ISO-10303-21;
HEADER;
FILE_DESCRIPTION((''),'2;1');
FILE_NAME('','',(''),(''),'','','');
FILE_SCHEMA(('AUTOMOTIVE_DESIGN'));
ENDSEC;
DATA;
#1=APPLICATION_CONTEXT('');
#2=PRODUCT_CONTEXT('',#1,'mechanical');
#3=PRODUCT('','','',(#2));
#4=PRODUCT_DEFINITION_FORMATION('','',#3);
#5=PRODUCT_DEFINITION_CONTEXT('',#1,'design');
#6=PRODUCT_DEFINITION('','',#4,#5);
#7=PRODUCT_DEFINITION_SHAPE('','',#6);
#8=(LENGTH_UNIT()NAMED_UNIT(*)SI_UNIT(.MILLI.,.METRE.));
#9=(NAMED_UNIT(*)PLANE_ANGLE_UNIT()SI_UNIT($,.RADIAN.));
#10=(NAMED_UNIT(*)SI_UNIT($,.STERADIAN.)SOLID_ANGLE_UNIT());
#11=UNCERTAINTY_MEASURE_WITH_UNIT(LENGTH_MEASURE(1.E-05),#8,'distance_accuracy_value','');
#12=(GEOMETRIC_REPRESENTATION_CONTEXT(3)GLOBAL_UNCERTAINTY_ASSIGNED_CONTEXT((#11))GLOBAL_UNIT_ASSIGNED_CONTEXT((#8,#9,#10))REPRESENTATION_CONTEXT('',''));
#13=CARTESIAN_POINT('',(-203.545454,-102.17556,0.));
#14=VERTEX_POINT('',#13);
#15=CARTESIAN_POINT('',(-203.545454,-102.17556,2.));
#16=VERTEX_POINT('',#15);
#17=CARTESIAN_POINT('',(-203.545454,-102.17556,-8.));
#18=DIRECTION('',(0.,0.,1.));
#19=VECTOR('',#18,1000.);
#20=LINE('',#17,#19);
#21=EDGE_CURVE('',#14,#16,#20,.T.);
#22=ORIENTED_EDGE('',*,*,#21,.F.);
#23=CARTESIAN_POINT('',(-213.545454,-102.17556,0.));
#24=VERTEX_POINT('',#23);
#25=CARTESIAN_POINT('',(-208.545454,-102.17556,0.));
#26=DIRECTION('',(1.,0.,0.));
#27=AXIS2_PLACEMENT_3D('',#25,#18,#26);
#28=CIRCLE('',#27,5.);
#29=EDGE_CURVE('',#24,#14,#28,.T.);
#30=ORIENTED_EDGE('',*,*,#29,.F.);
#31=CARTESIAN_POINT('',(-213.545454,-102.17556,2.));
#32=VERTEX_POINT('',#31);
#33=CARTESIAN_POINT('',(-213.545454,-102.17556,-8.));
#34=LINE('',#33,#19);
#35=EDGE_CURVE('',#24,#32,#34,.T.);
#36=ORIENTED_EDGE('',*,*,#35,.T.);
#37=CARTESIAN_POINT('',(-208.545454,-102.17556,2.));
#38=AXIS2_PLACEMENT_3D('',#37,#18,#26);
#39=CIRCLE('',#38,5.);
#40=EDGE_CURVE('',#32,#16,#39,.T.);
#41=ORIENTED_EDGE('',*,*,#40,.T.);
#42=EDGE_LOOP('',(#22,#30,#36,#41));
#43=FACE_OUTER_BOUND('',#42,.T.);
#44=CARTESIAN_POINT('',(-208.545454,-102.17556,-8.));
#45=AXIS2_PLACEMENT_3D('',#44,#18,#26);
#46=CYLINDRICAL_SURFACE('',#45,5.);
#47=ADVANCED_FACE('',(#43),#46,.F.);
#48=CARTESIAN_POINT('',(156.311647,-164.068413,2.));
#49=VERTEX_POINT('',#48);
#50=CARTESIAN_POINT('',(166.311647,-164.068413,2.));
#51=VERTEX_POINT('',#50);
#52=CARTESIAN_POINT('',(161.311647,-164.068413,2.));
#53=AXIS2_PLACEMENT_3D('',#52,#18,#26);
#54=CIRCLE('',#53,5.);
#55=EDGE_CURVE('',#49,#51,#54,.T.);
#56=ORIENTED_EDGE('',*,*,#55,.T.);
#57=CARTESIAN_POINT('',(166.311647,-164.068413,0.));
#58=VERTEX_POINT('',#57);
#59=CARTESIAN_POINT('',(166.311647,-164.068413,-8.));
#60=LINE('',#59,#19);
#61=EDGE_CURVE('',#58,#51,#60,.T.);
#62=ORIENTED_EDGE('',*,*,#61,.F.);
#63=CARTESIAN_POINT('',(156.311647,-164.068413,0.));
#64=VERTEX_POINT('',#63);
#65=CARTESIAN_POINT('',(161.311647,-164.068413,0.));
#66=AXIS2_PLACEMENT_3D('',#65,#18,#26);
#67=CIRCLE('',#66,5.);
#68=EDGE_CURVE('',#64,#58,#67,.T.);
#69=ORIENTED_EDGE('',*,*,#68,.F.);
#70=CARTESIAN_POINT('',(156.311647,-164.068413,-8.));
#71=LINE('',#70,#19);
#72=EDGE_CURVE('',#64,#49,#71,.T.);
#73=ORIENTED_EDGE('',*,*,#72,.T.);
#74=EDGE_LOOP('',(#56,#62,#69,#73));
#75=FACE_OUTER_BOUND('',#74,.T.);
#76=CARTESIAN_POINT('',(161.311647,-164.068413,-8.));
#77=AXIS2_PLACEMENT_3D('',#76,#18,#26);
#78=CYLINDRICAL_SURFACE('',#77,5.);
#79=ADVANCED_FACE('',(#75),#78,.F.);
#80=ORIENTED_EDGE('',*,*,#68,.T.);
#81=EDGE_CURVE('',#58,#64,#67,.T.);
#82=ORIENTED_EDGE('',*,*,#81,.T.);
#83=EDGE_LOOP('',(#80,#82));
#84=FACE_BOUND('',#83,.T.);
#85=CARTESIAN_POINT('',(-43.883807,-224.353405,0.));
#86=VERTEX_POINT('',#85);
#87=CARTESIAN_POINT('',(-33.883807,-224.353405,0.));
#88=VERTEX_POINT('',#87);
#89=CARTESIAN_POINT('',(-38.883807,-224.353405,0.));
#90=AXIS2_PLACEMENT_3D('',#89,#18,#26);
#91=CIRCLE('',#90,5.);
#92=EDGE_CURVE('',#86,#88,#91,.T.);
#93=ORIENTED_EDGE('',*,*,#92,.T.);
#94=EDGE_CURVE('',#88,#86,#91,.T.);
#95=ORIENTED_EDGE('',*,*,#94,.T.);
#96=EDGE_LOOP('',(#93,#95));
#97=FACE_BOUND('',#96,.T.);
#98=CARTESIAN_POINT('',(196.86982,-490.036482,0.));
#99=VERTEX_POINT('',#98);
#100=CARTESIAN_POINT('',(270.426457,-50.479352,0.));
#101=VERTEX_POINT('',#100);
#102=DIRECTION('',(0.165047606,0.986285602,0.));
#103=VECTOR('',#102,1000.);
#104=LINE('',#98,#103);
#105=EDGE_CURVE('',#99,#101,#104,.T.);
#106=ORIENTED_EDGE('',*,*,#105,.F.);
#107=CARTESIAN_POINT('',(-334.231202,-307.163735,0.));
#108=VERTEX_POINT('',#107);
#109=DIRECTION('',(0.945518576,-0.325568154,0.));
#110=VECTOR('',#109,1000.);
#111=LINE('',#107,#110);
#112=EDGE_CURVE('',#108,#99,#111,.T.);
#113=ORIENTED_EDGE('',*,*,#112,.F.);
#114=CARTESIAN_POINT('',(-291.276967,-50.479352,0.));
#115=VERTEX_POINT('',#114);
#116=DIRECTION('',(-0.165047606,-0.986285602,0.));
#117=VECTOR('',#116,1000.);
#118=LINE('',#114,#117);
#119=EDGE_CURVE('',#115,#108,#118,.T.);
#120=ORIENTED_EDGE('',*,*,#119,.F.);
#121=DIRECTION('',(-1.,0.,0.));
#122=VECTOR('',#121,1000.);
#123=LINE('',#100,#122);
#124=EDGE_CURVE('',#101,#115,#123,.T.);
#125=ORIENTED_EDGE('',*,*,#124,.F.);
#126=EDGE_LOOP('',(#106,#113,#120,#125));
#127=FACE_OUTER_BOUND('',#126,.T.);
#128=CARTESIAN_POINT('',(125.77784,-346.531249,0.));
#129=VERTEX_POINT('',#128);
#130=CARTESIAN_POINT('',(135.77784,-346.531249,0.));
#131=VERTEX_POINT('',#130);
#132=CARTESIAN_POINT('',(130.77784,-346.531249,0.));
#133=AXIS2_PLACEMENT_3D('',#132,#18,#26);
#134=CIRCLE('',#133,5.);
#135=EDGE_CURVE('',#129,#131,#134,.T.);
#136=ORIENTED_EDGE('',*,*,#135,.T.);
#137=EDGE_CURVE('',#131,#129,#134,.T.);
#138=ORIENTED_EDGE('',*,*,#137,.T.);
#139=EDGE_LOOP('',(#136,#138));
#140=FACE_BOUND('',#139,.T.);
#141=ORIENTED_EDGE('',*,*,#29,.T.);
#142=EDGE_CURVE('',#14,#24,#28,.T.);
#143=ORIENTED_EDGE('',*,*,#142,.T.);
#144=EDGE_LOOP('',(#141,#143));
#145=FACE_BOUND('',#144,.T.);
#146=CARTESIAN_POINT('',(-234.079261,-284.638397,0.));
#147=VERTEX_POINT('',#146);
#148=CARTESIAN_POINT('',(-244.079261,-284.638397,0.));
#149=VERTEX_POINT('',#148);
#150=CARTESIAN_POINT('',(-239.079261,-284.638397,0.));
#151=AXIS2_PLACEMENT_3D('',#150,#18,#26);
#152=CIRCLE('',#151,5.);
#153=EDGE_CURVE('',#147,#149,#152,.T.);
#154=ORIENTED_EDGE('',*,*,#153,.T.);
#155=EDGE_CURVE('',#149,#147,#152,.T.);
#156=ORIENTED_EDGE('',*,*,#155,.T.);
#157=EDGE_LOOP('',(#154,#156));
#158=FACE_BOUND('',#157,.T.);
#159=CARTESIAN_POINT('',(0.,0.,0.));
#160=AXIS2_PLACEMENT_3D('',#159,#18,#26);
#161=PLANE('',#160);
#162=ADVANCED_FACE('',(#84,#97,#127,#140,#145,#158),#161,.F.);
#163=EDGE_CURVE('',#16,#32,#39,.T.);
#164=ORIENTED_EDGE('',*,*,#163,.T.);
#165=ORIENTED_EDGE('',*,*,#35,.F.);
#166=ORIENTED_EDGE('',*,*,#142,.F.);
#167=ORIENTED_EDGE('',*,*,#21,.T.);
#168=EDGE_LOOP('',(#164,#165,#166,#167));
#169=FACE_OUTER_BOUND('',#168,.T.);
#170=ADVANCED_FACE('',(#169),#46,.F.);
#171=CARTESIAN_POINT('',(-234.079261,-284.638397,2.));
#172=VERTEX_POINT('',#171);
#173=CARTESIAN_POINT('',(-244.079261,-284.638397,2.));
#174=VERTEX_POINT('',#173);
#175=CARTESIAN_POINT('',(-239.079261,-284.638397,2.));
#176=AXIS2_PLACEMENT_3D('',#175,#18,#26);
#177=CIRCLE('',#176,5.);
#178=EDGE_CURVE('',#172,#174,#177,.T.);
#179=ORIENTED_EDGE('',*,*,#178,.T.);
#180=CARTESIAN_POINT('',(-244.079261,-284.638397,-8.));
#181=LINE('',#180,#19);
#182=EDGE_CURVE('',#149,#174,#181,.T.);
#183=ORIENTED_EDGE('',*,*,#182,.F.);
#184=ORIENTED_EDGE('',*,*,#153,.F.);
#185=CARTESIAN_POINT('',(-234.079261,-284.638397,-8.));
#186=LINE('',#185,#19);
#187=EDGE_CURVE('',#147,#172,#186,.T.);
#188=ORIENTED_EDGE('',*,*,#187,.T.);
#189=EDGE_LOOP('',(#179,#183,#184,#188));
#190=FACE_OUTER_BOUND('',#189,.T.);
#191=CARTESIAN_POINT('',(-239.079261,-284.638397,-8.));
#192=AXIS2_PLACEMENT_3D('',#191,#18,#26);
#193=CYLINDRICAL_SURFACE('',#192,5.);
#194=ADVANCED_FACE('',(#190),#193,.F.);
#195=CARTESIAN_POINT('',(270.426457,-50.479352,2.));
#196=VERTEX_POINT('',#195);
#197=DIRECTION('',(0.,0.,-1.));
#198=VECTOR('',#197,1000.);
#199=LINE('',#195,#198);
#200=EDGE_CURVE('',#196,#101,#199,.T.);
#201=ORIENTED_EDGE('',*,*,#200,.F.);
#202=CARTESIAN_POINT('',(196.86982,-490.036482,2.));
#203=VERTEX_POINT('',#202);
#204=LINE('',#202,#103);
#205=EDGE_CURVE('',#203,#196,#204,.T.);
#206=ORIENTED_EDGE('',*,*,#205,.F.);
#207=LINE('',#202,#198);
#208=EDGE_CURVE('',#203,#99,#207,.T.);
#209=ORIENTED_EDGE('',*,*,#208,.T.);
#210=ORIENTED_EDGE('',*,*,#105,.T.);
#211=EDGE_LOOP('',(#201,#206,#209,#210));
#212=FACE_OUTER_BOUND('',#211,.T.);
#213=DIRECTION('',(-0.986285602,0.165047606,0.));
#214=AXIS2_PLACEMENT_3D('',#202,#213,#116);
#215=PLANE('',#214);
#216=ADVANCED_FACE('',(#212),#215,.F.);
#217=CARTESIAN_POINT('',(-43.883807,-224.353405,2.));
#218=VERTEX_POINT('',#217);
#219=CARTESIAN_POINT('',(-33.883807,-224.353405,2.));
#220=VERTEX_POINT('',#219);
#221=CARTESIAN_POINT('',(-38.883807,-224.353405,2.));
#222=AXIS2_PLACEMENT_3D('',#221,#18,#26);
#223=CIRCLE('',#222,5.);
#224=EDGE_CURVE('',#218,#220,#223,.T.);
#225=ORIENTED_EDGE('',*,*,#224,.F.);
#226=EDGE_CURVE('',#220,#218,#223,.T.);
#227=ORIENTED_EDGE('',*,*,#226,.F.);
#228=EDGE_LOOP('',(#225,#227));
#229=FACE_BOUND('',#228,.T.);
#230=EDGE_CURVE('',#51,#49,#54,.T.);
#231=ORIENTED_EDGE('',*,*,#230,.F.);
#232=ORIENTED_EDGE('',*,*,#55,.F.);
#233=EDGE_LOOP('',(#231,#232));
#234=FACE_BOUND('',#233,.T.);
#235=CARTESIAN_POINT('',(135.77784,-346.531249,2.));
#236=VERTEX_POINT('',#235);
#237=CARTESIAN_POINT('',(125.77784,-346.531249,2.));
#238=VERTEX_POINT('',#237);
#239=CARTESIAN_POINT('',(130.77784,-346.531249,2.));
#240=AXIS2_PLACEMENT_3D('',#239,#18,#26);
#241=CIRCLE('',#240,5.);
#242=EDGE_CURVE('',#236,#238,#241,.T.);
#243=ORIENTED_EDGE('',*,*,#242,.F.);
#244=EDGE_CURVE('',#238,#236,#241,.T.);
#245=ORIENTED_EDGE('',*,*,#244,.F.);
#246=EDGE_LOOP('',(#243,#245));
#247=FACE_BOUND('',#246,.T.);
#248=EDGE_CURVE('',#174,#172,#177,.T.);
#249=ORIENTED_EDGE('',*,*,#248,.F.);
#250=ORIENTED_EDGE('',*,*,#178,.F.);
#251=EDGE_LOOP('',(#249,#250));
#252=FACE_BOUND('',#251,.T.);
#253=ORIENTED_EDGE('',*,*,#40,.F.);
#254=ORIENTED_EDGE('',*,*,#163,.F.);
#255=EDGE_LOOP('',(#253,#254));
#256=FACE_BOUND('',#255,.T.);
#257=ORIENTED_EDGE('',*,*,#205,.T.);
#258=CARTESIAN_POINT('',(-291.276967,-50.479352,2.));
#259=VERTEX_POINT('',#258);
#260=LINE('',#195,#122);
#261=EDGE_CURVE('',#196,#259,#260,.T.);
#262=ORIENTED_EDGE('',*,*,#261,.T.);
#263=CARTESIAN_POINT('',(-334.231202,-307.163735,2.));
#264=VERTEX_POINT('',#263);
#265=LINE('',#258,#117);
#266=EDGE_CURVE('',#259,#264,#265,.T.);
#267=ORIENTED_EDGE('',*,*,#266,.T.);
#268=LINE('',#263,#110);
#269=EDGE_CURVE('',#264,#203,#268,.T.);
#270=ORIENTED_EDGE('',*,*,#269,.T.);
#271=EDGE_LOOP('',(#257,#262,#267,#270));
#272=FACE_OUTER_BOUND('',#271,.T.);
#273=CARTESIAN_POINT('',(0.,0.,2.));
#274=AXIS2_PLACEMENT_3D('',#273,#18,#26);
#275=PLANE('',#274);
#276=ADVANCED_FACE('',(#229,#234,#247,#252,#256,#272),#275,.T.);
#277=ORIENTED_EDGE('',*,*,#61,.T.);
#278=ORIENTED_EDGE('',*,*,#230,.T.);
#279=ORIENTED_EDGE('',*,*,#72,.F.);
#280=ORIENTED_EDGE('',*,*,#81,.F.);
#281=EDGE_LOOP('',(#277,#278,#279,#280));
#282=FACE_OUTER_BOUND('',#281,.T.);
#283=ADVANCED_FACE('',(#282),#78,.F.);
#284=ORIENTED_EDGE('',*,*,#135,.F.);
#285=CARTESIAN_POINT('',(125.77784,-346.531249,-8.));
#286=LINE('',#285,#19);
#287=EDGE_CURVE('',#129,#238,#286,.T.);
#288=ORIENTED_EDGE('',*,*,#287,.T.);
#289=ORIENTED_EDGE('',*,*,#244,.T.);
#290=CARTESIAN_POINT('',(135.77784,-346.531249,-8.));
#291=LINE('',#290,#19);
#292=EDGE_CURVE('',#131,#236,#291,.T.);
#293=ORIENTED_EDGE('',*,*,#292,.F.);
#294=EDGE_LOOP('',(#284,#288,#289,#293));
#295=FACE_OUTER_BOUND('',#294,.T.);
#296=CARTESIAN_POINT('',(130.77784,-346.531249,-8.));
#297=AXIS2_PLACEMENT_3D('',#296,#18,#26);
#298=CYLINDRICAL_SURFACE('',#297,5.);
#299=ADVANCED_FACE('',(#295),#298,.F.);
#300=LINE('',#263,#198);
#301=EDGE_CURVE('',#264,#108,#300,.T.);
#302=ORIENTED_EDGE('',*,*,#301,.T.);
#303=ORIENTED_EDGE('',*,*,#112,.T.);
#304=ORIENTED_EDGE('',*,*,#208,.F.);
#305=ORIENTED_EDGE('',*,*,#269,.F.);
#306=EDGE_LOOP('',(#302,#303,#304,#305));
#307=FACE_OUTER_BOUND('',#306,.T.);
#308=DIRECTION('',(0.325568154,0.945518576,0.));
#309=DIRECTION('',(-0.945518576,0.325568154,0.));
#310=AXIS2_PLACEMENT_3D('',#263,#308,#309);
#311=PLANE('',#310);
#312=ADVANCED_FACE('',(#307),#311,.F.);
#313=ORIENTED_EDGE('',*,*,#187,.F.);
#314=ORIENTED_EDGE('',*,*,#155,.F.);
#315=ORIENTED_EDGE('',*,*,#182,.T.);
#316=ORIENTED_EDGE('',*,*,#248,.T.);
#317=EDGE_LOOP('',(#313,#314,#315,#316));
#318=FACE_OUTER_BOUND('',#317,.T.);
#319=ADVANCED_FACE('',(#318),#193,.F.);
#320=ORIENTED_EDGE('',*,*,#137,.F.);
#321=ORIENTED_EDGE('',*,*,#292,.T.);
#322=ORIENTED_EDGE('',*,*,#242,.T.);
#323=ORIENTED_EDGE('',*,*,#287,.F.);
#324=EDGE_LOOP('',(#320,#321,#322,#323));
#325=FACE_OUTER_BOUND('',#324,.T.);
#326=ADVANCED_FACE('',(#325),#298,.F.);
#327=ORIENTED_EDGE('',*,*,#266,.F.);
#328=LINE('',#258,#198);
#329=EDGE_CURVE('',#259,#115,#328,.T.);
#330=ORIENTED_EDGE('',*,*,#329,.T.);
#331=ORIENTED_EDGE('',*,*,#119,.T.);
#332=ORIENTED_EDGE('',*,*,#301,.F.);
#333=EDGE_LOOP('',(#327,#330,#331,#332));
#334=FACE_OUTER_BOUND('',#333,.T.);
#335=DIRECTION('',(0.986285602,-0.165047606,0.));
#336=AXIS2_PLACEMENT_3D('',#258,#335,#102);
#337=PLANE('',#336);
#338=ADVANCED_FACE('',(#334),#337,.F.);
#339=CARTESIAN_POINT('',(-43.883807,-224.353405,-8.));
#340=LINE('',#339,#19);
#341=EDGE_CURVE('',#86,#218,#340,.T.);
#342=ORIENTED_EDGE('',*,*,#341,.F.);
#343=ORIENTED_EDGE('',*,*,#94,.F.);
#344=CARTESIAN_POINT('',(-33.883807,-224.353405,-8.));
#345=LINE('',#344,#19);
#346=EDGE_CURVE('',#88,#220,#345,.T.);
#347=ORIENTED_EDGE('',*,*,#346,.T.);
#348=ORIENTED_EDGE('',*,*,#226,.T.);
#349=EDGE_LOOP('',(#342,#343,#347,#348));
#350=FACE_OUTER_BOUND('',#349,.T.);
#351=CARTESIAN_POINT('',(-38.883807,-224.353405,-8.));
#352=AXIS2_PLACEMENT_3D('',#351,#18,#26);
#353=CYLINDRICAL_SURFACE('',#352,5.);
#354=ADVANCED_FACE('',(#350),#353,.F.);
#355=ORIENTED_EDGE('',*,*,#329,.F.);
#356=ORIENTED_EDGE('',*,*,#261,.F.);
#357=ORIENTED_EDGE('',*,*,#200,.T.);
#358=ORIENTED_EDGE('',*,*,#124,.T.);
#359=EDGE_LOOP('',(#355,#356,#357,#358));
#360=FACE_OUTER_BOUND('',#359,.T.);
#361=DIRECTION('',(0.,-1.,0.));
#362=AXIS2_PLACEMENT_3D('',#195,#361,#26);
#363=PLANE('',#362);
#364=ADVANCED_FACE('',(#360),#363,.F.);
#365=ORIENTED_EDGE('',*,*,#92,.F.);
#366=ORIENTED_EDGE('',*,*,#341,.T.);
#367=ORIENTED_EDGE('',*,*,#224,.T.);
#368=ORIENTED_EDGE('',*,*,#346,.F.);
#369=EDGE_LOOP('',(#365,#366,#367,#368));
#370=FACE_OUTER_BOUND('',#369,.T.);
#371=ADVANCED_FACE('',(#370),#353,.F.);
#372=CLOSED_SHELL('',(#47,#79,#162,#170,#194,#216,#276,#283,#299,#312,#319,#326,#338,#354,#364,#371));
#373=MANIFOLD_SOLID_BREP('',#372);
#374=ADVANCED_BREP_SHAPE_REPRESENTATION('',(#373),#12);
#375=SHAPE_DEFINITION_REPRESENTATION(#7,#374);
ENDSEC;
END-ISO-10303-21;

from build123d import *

# Parameters (mm, degrees)
EXTRUDE_1_DEPTH     = 2
SKETCH_2_R          = 5
CUT_EXTRUDE_1_DEPTH = 10


with BuildPart() as part:
    # 草图1 → 凸台-拉伸1 (new body)
    with BuildSketch(Plane.XY):
        Polygon((270.4264573, -50.479352133), (-291.276967283, -50.479352133), (-334.231201576, -307.163734724), (196.869820345, -490.036482017), align=None)
    extrude(amount=EXTRUDE_1_DEPTH)

    # 草图2 → 切除-拉伸1 (cut)
    with BuildSketch(Plane.XY.offset(2)):
        with Locations((-208.545453815, -102.175560394)):
            Circle(SKETCH_2_R)
        with Locations((-239.079260899, -284.638396678)):
            Circle(SKETCH_2_R)
        with Locations((-38.883807069, -224.353404635)):
            Circle(SKETCH_2_R)
        with Locations((130.777839678, -346.531248876)):
            Circle(SKETCH_2_R)
        with Locations((161.311646762, -164.068412591)):
            Circle(SKETCH_2_R)
    extrude(amount=-CUT_EXTRUDE_1_DEPTH, mode=Mode.SUBTRACT)


solid = part.part
